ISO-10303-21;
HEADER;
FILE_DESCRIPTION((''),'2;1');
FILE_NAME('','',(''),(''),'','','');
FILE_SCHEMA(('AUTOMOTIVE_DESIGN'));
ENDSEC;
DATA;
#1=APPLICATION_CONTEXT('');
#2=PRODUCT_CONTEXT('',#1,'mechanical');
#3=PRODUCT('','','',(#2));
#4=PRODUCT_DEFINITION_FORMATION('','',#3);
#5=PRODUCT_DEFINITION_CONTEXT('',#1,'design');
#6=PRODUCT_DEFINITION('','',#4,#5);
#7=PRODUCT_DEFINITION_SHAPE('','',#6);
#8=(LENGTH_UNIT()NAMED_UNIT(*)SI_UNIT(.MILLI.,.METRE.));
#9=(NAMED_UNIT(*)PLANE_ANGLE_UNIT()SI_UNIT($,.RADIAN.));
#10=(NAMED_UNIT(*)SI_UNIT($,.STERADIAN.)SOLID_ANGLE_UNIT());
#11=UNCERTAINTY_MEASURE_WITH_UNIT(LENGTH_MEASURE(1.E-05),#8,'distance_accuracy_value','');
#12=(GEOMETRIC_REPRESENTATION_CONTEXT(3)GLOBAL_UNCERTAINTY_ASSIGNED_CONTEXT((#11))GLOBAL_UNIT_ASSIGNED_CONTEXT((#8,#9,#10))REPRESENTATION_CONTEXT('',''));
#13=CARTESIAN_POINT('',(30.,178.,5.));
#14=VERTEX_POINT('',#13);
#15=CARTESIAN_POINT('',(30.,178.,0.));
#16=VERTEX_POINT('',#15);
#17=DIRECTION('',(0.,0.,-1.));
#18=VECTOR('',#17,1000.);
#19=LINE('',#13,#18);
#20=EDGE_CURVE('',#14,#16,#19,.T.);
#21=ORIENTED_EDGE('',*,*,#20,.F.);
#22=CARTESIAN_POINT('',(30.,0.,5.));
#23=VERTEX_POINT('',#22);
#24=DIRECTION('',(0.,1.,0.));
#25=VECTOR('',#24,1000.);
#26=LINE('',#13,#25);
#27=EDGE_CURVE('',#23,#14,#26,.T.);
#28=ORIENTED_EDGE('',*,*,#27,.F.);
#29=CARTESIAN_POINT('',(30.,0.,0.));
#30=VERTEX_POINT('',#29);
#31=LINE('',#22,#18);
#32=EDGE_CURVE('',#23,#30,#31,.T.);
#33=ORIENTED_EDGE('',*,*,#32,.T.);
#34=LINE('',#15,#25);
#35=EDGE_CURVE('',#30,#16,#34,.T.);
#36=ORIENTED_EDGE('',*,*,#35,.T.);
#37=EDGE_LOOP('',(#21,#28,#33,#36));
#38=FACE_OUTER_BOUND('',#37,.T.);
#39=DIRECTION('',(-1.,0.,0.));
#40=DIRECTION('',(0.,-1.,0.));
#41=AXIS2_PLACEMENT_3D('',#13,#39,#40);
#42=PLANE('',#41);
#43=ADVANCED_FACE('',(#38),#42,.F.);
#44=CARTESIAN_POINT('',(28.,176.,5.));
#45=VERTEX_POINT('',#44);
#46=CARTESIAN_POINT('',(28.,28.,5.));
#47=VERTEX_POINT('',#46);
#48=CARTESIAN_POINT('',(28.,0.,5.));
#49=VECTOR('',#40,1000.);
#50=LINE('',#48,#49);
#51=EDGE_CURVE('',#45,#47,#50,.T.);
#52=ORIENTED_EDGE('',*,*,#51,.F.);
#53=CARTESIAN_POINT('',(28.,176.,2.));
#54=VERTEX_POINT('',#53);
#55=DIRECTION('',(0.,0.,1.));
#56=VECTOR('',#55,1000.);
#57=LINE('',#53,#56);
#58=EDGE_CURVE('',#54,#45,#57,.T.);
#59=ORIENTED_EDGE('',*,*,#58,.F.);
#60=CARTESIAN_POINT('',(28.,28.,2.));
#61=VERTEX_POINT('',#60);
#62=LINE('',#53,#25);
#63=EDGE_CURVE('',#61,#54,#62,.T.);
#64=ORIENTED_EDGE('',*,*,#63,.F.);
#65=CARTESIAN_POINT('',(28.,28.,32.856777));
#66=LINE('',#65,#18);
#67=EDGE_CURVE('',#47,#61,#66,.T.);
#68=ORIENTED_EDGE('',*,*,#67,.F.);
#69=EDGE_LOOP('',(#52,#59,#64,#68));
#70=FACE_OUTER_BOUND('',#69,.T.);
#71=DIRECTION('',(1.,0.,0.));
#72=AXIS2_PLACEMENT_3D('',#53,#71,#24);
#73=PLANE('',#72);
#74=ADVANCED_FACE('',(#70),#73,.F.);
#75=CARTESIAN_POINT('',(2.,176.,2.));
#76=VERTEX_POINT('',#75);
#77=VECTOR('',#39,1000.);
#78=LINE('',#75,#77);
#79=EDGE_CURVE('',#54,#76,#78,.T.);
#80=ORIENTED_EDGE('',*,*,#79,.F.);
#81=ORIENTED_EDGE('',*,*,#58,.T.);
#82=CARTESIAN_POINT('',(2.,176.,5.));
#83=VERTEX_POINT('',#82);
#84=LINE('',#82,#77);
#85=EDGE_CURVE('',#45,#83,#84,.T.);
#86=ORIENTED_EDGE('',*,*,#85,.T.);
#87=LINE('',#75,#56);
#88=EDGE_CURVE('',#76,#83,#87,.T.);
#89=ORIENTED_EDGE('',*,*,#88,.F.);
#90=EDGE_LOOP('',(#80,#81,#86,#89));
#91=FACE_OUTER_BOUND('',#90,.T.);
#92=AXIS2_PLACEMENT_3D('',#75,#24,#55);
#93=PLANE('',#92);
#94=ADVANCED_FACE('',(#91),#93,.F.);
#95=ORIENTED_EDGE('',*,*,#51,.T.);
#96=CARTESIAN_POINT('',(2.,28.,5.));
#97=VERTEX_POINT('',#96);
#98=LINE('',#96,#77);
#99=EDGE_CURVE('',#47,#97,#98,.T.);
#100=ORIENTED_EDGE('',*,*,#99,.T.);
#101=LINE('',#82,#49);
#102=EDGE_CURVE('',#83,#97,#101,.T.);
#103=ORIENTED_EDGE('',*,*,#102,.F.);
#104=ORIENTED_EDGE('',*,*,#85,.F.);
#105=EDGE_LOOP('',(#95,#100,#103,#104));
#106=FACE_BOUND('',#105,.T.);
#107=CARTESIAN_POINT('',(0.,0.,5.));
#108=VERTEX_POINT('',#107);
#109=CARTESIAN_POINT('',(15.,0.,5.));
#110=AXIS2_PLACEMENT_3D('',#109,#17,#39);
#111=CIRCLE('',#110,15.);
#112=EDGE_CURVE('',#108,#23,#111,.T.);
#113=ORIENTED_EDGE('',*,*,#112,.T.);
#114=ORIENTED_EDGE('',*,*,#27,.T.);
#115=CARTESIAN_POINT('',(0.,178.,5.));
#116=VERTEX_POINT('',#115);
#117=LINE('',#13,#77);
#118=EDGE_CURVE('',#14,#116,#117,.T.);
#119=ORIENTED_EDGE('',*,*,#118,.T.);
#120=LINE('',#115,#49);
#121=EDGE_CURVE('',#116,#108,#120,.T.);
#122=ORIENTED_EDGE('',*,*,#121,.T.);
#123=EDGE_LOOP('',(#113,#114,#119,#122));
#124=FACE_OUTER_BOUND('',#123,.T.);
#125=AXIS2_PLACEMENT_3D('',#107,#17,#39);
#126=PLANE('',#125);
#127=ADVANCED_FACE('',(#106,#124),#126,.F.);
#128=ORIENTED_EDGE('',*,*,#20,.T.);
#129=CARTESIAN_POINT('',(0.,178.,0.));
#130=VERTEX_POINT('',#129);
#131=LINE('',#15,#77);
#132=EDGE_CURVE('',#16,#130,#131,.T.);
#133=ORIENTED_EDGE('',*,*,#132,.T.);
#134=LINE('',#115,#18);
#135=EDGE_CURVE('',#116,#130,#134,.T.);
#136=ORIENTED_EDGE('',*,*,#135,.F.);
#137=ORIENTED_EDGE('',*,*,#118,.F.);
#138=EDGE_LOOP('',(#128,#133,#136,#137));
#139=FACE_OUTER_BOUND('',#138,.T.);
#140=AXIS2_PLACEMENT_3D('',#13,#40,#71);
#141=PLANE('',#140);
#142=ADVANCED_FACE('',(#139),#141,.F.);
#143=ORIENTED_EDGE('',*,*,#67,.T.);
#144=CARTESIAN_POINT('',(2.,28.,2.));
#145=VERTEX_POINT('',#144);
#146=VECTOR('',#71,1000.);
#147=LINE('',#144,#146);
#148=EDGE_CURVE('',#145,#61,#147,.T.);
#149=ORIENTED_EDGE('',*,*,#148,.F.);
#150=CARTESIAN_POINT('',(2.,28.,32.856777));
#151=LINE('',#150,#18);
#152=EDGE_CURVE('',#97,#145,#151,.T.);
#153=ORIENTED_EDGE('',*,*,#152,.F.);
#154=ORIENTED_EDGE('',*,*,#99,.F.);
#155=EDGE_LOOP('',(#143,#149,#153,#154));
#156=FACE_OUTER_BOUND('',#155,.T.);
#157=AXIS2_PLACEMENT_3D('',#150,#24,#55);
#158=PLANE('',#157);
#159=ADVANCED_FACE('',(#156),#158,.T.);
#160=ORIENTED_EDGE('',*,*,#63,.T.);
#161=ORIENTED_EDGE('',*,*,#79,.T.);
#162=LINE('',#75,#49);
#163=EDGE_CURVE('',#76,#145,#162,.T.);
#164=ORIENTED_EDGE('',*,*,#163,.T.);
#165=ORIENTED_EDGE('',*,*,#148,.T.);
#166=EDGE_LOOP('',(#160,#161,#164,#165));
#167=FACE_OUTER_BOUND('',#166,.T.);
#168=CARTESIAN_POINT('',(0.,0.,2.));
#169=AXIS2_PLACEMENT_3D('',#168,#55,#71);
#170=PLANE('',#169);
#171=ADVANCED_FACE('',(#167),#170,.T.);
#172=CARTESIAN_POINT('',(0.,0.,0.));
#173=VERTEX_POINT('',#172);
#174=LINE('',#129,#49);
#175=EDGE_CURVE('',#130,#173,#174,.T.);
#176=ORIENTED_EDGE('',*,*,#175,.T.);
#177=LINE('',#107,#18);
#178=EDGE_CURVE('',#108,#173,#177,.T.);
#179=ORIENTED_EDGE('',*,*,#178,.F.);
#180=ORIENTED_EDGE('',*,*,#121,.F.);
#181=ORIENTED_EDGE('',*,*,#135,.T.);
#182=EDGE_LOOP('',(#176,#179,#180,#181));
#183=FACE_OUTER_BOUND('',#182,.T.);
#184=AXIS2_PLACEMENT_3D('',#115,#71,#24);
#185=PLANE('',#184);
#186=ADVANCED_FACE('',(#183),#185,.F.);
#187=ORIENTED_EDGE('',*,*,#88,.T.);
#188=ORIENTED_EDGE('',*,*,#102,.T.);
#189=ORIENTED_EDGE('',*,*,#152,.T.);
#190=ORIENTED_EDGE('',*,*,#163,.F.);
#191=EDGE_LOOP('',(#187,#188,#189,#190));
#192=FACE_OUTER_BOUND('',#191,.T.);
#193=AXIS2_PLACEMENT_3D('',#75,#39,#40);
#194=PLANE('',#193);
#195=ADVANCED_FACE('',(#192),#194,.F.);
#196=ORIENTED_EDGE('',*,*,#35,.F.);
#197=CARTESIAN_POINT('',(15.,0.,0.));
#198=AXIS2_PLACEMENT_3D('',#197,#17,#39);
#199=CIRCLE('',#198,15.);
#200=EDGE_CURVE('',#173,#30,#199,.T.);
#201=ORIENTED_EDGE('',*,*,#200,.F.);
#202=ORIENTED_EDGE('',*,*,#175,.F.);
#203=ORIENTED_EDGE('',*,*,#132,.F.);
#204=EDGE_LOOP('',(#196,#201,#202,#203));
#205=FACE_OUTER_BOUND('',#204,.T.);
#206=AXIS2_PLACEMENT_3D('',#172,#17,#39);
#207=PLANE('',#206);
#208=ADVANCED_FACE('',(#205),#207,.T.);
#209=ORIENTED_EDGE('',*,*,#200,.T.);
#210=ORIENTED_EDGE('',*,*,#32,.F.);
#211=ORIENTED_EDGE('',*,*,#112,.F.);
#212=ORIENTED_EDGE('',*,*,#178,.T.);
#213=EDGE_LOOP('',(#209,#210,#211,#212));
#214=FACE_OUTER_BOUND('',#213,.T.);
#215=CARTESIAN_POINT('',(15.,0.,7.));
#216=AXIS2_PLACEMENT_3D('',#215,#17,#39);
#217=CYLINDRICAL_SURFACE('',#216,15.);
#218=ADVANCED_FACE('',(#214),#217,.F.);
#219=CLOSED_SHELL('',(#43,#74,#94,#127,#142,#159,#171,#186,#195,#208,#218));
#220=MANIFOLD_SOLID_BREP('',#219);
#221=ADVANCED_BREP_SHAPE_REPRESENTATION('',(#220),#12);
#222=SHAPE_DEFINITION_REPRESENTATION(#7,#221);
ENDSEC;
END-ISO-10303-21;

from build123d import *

# Parameters (mm, degrees)
SKETCH1_W           = 30
SKETCH1_H           = 178
BOSS_EXTRUDE1_DEPTH = 5
SKETCH3_W           = 26
SKETCH3_H           = 210
CUT_EXTRUDE1_DEPTH  = 3
SKETCH4_W           = 26
SKETCH4_H           = 10
BOSS_EXTRUDE2_DEPTH = 3
CUT_EXTRUDE3_DEPTH  = 5
BOSS_EXTRUDE3_START = 3
BOSS_EXTRUDE3_DEPTH = 3


with BuildPart() as part:
    # Sketch1 → Boss-Extrude1 (new body)
    with BuildSketch(Plane.XY):
        with Locations((15, 89)):
            Rectangle(SKETCH1_W, SKETCH1_H)
    extrude(amount=BOSS_EXTRUDE1_DEPTH)

    # Sketch3 → Cut-Extrude1 (cut)
    with BuildSketch(Plane.XY.offset(5)):
        with Locations((15, 71)):
            Rectangle(SKETCH3_W, SKETCH3_H)
    extrude(amount=-CUT_EXTRUDE1_DEPTH, mode=Mode.SUBTRACT)

    # Sketch4 → Boss-Extrude2 (add)
    with BuildSketch(Plane.XY.offset(2)):
        with Locations((15, 23)):
            Rectangle(SKETCH4_W, SKETCH4_H)
    extrude(amount=BOSS_EXTRUDE2_DEPTH)

    # Sketch5 → Cut-Extrude3 (cut, symmetric)
    with BuildSketch(Plane.XY.offset(2)):
        with BuildLine():
            Line((0, 0), (30, 0))
            ThreePointArc((30, 0), (15, 15), (0, 0))
        make_face()
    extrude(amount=CUT_EXTRUDE3_DEPTH, both=True, mode=Mode.SUBTRACT)

    # Sketch6 → Boss-Extrude3 (add)
    with BuildSketch(Plane.XY.offset(2).offset(BOSS_EXTRUDE3_START)):
        with BuildLine():
            Line((28, 7.483314774), (28, 18))
            Line((28, 18), (2, 18))
            Line((2, 18), (2, 7.483314774))
            ThreePointArc((2, 7.483314774), (15, 15), (28, 7.483314774))
        make_face()
    extrude(amount=-BOSS_EXTRUDE3_DEPTH)


solid = part.part
